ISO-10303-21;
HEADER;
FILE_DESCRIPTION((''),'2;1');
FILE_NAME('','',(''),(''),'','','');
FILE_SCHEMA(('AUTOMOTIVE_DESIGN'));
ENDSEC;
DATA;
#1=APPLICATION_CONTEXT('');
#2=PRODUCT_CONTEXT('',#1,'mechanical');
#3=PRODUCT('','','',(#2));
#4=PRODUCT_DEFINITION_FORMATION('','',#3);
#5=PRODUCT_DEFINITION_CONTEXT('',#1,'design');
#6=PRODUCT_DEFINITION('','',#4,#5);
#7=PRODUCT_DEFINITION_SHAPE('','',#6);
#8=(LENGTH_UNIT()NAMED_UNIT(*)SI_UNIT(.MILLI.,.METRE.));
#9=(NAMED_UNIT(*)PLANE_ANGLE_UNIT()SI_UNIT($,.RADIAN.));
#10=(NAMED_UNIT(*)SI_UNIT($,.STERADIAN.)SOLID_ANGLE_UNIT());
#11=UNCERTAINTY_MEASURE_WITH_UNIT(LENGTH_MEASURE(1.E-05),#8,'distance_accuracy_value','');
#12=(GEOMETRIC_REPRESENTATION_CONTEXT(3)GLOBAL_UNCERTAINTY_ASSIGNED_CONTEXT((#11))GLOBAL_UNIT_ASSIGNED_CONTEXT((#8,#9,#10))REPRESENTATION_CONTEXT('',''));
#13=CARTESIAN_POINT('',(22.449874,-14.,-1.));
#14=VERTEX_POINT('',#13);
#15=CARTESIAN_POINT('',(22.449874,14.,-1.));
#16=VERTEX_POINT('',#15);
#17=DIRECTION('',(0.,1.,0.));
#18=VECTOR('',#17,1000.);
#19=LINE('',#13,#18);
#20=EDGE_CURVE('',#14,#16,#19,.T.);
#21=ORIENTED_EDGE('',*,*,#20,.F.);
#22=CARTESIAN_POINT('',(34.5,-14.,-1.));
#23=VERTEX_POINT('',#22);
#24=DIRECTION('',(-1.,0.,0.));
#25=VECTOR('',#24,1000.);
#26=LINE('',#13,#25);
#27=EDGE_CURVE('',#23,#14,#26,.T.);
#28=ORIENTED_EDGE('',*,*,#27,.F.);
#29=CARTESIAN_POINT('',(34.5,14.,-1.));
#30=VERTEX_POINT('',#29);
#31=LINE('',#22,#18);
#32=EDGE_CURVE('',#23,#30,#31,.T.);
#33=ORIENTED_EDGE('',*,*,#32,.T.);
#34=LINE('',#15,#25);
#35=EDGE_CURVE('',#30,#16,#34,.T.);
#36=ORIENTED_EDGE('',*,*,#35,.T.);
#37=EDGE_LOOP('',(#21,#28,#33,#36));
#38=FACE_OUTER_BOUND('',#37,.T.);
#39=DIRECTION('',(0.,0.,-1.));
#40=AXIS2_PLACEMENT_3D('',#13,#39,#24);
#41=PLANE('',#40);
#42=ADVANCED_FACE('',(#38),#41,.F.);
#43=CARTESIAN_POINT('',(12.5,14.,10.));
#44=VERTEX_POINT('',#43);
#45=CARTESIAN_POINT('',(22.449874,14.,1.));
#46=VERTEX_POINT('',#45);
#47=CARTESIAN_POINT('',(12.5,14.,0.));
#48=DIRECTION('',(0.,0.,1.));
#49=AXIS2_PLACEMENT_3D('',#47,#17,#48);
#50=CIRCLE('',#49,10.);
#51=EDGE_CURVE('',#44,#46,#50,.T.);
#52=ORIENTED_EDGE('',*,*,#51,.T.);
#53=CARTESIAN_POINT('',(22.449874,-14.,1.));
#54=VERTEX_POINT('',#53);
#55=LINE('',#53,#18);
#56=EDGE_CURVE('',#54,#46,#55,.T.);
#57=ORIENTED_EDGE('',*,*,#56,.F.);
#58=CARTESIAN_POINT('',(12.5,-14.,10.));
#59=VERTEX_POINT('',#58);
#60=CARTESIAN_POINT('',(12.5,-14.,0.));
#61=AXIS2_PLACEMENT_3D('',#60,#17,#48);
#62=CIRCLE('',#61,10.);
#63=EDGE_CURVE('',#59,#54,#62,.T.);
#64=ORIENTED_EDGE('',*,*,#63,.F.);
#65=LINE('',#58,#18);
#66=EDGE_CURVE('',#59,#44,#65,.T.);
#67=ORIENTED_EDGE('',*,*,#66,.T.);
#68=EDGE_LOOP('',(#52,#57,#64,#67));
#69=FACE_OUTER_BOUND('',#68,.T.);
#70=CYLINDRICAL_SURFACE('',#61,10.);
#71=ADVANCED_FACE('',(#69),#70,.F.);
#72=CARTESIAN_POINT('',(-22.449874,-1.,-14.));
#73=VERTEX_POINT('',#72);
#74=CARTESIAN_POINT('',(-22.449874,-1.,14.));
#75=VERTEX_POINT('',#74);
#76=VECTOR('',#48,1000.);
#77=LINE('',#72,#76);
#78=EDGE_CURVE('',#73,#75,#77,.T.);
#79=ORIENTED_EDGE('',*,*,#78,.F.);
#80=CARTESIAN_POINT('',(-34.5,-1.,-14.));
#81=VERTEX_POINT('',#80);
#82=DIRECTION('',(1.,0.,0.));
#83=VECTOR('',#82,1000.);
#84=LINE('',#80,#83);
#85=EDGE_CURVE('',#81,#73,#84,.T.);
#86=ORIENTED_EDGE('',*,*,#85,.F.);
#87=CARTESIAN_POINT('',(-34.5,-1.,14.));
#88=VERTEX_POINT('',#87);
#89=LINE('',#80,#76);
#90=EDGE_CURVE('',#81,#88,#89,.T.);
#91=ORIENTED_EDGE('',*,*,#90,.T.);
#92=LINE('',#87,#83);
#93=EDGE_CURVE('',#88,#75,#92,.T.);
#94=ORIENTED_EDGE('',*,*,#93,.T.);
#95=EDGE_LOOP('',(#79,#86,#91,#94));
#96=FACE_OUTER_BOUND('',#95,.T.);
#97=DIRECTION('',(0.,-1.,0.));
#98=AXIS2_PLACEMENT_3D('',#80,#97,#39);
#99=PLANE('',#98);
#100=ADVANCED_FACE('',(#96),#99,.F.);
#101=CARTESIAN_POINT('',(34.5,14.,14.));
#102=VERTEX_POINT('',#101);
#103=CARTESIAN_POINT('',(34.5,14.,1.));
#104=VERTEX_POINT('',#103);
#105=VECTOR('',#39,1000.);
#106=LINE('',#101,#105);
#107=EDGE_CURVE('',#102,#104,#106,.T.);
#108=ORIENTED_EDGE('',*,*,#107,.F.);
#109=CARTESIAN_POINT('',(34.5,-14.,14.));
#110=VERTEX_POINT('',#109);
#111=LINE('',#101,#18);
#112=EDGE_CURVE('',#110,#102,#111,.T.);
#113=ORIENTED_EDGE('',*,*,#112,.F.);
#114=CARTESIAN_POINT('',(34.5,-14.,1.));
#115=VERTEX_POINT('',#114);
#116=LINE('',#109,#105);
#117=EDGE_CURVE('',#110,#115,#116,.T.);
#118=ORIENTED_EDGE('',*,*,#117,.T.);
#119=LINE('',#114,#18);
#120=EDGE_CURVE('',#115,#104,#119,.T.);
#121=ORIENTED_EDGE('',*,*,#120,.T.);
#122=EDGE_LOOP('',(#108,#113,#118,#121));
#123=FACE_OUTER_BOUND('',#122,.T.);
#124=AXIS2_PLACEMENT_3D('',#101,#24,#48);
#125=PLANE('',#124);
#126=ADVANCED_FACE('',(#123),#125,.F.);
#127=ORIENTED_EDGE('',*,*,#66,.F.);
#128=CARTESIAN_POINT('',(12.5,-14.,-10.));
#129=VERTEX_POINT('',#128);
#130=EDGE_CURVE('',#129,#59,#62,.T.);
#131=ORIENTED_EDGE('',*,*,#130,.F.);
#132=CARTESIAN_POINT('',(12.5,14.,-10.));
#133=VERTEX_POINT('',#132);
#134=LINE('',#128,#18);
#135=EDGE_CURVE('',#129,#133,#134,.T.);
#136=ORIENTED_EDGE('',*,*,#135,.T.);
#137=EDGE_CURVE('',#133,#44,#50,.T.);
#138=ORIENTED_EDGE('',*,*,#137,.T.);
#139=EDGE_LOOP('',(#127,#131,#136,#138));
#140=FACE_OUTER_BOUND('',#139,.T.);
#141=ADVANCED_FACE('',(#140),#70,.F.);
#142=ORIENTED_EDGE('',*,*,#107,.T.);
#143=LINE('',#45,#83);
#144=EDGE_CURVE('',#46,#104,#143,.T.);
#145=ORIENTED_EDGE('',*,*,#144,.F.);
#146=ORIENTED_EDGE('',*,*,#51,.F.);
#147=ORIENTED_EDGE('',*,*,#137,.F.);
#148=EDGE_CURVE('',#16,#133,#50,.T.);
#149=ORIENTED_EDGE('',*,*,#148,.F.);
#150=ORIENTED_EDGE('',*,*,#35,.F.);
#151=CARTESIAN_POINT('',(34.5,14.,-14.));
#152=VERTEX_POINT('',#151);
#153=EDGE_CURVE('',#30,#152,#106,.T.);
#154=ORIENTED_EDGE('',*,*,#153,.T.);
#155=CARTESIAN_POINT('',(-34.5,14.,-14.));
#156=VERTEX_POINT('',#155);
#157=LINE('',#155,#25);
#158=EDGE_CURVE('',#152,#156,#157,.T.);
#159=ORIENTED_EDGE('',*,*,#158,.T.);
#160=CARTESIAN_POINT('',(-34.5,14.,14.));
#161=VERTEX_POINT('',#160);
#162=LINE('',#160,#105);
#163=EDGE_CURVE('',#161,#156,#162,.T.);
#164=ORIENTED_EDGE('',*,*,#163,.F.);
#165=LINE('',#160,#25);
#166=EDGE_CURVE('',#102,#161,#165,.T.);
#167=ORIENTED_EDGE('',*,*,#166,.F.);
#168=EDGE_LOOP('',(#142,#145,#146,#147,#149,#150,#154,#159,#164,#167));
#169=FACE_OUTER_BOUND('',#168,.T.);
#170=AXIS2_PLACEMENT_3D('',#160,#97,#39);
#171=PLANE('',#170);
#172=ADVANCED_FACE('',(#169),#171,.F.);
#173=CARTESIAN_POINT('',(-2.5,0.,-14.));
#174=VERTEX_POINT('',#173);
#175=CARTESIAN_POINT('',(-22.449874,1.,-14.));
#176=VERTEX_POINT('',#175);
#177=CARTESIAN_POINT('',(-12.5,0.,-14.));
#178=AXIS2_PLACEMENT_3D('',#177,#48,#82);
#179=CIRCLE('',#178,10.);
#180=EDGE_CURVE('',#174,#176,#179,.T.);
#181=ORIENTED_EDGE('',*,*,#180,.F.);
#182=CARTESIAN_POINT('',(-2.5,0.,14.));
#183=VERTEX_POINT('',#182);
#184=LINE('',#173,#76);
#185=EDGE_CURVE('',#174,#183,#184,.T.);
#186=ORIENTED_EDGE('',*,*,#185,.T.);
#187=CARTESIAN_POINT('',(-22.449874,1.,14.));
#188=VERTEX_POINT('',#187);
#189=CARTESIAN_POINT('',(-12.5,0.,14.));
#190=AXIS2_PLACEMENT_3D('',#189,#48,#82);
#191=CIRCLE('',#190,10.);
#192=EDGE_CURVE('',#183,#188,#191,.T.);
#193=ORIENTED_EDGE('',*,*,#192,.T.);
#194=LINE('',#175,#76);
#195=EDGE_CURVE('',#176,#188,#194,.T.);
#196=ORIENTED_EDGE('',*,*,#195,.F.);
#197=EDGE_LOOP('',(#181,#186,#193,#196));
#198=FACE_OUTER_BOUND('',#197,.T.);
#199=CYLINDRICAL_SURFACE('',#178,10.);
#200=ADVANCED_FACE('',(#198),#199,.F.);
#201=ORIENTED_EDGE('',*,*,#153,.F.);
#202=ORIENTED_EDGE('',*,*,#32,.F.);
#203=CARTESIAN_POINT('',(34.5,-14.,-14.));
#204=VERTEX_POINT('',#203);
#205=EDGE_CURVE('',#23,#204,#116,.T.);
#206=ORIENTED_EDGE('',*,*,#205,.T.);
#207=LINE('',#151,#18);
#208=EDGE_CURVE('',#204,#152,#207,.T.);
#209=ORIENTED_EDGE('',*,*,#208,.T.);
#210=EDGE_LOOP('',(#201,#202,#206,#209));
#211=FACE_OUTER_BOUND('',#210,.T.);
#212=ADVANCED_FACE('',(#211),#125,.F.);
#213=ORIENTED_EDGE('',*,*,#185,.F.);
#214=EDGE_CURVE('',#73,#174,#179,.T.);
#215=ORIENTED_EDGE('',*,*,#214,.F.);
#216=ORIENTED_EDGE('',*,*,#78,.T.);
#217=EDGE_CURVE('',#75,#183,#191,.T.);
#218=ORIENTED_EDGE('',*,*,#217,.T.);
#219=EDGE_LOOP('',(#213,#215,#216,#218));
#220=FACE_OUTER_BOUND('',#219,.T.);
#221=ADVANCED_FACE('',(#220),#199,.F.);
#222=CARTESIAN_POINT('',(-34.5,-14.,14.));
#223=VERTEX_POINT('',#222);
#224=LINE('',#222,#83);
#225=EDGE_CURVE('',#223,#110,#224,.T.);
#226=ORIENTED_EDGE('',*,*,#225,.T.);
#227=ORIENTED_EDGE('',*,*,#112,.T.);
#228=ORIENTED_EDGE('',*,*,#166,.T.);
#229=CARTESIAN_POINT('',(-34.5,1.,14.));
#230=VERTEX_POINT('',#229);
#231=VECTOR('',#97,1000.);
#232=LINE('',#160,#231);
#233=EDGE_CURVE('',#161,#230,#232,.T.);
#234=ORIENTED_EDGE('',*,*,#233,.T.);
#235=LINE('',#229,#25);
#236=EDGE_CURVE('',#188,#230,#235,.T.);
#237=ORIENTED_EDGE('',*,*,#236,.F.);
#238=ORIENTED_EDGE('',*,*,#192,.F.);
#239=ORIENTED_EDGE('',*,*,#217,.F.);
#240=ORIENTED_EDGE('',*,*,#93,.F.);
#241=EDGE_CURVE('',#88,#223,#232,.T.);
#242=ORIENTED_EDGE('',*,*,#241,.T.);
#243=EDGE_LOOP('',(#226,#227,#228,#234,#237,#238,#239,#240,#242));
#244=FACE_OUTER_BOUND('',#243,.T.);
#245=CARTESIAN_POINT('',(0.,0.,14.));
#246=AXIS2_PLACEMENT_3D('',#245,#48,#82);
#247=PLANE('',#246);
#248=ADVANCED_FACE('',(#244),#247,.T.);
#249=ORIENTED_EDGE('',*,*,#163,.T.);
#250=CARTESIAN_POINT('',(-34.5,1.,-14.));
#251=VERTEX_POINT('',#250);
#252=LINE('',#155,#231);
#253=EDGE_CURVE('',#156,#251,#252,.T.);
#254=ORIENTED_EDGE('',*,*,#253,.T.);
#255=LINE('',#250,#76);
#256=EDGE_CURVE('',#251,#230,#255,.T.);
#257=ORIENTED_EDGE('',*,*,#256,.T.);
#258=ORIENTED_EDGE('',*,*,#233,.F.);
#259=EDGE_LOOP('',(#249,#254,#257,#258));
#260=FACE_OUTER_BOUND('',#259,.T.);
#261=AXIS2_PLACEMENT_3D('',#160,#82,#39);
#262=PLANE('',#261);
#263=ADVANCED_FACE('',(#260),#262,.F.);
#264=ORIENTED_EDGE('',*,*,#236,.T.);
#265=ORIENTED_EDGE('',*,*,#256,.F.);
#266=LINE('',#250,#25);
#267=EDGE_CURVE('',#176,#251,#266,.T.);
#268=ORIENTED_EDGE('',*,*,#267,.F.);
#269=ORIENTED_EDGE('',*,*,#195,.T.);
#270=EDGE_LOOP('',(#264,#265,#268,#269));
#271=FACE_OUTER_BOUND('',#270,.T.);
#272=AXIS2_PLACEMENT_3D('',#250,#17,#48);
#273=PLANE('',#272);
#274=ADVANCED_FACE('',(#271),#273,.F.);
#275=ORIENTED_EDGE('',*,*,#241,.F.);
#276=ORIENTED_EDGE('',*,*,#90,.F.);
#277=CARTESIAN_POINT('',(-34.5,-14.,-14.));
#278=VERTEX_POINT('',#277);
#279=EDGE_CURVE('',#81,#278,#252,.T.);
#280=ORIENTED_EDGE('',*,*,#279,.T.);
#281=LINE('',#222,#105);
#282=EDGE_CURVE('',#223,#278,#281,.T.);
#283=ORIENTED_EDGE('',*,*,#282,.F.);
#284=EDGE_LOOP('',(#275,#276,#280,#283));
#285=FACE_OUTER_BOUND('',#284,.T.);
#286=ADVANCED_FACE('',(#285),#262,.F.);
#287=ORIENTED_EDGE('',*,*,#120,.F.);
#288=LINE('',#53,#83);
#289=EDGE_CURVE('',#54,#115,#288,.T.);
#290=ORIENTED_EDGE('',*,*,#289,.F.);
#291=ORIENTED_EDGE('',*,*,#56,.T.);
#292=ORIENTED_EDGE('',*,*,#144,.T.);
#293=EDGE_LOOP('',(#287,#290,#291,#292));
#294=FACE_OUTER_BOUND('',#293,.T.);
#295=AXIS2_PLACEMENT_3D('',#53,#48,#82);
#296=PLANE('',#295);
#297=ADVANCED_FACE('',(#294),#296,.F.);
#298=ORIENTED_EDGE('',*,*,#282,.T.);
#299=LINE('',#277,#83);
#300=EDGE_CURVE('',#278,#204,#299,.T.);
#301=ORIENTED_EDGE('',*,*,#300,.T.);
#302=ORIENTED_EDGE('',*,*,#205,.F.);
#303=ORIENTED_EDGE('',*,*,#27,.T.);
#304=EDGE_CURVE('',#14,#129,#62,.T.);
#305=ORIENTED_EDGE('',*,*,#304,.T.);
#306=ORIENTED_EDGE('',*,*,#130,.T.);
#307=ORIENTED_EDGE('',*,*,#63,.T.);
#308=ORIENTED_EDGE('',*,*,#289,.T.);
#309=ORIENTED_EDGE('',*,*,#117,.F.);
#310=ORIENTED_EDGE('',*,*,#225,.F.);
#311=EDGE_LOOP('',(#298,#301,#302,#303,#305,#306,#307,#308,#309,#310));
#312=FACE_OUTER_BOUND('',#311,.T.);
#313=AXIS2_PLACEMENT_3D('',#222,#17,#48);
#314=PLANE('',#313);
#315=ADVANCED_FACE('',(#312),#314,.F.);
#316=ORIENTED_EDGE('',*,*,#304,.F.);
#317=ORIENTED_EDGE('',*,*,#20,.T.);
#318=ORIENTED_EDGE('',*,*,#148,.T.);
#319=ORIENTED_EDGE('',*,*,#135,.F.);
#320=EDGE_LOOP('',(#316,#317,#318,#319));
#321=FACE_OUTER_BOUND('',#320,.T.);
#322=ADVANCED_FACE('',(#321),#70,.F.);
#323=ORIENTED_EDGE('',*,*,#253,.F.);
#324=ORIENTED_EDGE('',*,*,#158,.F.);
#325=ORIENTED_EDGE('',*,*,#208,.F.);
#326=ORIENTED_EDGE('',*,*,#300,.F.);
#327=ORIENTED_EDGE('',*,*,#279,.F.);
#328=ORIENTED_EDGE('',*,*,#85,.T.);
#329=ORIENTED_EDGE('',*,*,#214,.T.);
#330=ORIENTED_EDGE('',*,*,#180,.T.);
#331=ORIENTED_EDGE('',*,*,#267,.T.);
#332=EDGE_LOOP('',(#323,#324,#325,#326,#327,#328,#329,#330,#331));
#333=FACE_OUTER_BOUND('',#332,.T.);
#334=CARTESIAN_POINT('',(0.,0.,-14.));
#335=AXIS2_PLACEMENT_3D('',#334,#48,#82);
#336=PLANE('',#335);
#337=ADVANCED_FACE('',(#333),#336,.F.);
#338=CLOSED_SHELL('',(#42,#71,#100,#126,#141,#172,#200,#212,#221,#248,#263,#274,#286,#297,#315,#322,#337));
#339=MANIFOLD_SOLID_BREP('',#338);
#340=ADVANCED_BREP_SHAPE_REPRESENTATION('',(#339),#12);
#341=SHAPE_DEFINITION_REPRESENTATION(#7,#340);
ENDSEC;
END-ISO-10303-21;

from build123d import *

# Parameters (mm, degrees)
SKETCH_1_W          = 69
SKETCH_1_H          = 28
EXTRUDE_1_DEPTH     = 14
CUT_EXTRUDE_1_DEPTH = 47.585942086
CUT_EXTRUDE_2_DEPTH = 47.585942086


with BuildPart() as part:
    # 草图1 → 凸台-拉伸1 (new, symmetric)
    with BuildSketch(Plane.XY):
        Rectangle(SKETCH_1_W, SKETCH_1_H)
    extrude(amount=EXTRUDE_1_DEPTH, both=True)

    # 草图2 → 切除-拉伸1 (cut, through all)
    with BuildSketch(Plane.XY.offset(14)):
        with BuildLine():
            Line((-34.5, 1), (-22.449874371, 1))
            ThreePointArc((-22.449874371, 1), (-2.5, 0), (-22.449874371, -1))
            Line((-22.449874371, -1), (-34.5, -1))
            Line((-34.5, -1), (-34.5, 1))
        make_face()
    extrude(amount=-CUT_EXTRUDE_1_DEPTH, mode=Mode.SUBTRACT)

    # 草图3 → 切除-拉伸2 (cut, through all)
    with BuildSketch(Plane(origin=(0, 14, 0), x_dir=(1, 0, 0), z_dir=(0, 1, 0))):
        with BuildLine():
            Line((22.449874371, -1), (34.5, -1))
            Line((34.5, -1), (34.5, 1))
            Line((34.5, 1), (22.449874371, 1))
            ThreePointArc((22.449874371, 1), (2.5, 0), (22.449874371, -1))
        make_face()
    extrude(amount=-CUT_EXTRUDE_2_DEPTH, mode=Mode.SUBTRACT)


solid = part.part
